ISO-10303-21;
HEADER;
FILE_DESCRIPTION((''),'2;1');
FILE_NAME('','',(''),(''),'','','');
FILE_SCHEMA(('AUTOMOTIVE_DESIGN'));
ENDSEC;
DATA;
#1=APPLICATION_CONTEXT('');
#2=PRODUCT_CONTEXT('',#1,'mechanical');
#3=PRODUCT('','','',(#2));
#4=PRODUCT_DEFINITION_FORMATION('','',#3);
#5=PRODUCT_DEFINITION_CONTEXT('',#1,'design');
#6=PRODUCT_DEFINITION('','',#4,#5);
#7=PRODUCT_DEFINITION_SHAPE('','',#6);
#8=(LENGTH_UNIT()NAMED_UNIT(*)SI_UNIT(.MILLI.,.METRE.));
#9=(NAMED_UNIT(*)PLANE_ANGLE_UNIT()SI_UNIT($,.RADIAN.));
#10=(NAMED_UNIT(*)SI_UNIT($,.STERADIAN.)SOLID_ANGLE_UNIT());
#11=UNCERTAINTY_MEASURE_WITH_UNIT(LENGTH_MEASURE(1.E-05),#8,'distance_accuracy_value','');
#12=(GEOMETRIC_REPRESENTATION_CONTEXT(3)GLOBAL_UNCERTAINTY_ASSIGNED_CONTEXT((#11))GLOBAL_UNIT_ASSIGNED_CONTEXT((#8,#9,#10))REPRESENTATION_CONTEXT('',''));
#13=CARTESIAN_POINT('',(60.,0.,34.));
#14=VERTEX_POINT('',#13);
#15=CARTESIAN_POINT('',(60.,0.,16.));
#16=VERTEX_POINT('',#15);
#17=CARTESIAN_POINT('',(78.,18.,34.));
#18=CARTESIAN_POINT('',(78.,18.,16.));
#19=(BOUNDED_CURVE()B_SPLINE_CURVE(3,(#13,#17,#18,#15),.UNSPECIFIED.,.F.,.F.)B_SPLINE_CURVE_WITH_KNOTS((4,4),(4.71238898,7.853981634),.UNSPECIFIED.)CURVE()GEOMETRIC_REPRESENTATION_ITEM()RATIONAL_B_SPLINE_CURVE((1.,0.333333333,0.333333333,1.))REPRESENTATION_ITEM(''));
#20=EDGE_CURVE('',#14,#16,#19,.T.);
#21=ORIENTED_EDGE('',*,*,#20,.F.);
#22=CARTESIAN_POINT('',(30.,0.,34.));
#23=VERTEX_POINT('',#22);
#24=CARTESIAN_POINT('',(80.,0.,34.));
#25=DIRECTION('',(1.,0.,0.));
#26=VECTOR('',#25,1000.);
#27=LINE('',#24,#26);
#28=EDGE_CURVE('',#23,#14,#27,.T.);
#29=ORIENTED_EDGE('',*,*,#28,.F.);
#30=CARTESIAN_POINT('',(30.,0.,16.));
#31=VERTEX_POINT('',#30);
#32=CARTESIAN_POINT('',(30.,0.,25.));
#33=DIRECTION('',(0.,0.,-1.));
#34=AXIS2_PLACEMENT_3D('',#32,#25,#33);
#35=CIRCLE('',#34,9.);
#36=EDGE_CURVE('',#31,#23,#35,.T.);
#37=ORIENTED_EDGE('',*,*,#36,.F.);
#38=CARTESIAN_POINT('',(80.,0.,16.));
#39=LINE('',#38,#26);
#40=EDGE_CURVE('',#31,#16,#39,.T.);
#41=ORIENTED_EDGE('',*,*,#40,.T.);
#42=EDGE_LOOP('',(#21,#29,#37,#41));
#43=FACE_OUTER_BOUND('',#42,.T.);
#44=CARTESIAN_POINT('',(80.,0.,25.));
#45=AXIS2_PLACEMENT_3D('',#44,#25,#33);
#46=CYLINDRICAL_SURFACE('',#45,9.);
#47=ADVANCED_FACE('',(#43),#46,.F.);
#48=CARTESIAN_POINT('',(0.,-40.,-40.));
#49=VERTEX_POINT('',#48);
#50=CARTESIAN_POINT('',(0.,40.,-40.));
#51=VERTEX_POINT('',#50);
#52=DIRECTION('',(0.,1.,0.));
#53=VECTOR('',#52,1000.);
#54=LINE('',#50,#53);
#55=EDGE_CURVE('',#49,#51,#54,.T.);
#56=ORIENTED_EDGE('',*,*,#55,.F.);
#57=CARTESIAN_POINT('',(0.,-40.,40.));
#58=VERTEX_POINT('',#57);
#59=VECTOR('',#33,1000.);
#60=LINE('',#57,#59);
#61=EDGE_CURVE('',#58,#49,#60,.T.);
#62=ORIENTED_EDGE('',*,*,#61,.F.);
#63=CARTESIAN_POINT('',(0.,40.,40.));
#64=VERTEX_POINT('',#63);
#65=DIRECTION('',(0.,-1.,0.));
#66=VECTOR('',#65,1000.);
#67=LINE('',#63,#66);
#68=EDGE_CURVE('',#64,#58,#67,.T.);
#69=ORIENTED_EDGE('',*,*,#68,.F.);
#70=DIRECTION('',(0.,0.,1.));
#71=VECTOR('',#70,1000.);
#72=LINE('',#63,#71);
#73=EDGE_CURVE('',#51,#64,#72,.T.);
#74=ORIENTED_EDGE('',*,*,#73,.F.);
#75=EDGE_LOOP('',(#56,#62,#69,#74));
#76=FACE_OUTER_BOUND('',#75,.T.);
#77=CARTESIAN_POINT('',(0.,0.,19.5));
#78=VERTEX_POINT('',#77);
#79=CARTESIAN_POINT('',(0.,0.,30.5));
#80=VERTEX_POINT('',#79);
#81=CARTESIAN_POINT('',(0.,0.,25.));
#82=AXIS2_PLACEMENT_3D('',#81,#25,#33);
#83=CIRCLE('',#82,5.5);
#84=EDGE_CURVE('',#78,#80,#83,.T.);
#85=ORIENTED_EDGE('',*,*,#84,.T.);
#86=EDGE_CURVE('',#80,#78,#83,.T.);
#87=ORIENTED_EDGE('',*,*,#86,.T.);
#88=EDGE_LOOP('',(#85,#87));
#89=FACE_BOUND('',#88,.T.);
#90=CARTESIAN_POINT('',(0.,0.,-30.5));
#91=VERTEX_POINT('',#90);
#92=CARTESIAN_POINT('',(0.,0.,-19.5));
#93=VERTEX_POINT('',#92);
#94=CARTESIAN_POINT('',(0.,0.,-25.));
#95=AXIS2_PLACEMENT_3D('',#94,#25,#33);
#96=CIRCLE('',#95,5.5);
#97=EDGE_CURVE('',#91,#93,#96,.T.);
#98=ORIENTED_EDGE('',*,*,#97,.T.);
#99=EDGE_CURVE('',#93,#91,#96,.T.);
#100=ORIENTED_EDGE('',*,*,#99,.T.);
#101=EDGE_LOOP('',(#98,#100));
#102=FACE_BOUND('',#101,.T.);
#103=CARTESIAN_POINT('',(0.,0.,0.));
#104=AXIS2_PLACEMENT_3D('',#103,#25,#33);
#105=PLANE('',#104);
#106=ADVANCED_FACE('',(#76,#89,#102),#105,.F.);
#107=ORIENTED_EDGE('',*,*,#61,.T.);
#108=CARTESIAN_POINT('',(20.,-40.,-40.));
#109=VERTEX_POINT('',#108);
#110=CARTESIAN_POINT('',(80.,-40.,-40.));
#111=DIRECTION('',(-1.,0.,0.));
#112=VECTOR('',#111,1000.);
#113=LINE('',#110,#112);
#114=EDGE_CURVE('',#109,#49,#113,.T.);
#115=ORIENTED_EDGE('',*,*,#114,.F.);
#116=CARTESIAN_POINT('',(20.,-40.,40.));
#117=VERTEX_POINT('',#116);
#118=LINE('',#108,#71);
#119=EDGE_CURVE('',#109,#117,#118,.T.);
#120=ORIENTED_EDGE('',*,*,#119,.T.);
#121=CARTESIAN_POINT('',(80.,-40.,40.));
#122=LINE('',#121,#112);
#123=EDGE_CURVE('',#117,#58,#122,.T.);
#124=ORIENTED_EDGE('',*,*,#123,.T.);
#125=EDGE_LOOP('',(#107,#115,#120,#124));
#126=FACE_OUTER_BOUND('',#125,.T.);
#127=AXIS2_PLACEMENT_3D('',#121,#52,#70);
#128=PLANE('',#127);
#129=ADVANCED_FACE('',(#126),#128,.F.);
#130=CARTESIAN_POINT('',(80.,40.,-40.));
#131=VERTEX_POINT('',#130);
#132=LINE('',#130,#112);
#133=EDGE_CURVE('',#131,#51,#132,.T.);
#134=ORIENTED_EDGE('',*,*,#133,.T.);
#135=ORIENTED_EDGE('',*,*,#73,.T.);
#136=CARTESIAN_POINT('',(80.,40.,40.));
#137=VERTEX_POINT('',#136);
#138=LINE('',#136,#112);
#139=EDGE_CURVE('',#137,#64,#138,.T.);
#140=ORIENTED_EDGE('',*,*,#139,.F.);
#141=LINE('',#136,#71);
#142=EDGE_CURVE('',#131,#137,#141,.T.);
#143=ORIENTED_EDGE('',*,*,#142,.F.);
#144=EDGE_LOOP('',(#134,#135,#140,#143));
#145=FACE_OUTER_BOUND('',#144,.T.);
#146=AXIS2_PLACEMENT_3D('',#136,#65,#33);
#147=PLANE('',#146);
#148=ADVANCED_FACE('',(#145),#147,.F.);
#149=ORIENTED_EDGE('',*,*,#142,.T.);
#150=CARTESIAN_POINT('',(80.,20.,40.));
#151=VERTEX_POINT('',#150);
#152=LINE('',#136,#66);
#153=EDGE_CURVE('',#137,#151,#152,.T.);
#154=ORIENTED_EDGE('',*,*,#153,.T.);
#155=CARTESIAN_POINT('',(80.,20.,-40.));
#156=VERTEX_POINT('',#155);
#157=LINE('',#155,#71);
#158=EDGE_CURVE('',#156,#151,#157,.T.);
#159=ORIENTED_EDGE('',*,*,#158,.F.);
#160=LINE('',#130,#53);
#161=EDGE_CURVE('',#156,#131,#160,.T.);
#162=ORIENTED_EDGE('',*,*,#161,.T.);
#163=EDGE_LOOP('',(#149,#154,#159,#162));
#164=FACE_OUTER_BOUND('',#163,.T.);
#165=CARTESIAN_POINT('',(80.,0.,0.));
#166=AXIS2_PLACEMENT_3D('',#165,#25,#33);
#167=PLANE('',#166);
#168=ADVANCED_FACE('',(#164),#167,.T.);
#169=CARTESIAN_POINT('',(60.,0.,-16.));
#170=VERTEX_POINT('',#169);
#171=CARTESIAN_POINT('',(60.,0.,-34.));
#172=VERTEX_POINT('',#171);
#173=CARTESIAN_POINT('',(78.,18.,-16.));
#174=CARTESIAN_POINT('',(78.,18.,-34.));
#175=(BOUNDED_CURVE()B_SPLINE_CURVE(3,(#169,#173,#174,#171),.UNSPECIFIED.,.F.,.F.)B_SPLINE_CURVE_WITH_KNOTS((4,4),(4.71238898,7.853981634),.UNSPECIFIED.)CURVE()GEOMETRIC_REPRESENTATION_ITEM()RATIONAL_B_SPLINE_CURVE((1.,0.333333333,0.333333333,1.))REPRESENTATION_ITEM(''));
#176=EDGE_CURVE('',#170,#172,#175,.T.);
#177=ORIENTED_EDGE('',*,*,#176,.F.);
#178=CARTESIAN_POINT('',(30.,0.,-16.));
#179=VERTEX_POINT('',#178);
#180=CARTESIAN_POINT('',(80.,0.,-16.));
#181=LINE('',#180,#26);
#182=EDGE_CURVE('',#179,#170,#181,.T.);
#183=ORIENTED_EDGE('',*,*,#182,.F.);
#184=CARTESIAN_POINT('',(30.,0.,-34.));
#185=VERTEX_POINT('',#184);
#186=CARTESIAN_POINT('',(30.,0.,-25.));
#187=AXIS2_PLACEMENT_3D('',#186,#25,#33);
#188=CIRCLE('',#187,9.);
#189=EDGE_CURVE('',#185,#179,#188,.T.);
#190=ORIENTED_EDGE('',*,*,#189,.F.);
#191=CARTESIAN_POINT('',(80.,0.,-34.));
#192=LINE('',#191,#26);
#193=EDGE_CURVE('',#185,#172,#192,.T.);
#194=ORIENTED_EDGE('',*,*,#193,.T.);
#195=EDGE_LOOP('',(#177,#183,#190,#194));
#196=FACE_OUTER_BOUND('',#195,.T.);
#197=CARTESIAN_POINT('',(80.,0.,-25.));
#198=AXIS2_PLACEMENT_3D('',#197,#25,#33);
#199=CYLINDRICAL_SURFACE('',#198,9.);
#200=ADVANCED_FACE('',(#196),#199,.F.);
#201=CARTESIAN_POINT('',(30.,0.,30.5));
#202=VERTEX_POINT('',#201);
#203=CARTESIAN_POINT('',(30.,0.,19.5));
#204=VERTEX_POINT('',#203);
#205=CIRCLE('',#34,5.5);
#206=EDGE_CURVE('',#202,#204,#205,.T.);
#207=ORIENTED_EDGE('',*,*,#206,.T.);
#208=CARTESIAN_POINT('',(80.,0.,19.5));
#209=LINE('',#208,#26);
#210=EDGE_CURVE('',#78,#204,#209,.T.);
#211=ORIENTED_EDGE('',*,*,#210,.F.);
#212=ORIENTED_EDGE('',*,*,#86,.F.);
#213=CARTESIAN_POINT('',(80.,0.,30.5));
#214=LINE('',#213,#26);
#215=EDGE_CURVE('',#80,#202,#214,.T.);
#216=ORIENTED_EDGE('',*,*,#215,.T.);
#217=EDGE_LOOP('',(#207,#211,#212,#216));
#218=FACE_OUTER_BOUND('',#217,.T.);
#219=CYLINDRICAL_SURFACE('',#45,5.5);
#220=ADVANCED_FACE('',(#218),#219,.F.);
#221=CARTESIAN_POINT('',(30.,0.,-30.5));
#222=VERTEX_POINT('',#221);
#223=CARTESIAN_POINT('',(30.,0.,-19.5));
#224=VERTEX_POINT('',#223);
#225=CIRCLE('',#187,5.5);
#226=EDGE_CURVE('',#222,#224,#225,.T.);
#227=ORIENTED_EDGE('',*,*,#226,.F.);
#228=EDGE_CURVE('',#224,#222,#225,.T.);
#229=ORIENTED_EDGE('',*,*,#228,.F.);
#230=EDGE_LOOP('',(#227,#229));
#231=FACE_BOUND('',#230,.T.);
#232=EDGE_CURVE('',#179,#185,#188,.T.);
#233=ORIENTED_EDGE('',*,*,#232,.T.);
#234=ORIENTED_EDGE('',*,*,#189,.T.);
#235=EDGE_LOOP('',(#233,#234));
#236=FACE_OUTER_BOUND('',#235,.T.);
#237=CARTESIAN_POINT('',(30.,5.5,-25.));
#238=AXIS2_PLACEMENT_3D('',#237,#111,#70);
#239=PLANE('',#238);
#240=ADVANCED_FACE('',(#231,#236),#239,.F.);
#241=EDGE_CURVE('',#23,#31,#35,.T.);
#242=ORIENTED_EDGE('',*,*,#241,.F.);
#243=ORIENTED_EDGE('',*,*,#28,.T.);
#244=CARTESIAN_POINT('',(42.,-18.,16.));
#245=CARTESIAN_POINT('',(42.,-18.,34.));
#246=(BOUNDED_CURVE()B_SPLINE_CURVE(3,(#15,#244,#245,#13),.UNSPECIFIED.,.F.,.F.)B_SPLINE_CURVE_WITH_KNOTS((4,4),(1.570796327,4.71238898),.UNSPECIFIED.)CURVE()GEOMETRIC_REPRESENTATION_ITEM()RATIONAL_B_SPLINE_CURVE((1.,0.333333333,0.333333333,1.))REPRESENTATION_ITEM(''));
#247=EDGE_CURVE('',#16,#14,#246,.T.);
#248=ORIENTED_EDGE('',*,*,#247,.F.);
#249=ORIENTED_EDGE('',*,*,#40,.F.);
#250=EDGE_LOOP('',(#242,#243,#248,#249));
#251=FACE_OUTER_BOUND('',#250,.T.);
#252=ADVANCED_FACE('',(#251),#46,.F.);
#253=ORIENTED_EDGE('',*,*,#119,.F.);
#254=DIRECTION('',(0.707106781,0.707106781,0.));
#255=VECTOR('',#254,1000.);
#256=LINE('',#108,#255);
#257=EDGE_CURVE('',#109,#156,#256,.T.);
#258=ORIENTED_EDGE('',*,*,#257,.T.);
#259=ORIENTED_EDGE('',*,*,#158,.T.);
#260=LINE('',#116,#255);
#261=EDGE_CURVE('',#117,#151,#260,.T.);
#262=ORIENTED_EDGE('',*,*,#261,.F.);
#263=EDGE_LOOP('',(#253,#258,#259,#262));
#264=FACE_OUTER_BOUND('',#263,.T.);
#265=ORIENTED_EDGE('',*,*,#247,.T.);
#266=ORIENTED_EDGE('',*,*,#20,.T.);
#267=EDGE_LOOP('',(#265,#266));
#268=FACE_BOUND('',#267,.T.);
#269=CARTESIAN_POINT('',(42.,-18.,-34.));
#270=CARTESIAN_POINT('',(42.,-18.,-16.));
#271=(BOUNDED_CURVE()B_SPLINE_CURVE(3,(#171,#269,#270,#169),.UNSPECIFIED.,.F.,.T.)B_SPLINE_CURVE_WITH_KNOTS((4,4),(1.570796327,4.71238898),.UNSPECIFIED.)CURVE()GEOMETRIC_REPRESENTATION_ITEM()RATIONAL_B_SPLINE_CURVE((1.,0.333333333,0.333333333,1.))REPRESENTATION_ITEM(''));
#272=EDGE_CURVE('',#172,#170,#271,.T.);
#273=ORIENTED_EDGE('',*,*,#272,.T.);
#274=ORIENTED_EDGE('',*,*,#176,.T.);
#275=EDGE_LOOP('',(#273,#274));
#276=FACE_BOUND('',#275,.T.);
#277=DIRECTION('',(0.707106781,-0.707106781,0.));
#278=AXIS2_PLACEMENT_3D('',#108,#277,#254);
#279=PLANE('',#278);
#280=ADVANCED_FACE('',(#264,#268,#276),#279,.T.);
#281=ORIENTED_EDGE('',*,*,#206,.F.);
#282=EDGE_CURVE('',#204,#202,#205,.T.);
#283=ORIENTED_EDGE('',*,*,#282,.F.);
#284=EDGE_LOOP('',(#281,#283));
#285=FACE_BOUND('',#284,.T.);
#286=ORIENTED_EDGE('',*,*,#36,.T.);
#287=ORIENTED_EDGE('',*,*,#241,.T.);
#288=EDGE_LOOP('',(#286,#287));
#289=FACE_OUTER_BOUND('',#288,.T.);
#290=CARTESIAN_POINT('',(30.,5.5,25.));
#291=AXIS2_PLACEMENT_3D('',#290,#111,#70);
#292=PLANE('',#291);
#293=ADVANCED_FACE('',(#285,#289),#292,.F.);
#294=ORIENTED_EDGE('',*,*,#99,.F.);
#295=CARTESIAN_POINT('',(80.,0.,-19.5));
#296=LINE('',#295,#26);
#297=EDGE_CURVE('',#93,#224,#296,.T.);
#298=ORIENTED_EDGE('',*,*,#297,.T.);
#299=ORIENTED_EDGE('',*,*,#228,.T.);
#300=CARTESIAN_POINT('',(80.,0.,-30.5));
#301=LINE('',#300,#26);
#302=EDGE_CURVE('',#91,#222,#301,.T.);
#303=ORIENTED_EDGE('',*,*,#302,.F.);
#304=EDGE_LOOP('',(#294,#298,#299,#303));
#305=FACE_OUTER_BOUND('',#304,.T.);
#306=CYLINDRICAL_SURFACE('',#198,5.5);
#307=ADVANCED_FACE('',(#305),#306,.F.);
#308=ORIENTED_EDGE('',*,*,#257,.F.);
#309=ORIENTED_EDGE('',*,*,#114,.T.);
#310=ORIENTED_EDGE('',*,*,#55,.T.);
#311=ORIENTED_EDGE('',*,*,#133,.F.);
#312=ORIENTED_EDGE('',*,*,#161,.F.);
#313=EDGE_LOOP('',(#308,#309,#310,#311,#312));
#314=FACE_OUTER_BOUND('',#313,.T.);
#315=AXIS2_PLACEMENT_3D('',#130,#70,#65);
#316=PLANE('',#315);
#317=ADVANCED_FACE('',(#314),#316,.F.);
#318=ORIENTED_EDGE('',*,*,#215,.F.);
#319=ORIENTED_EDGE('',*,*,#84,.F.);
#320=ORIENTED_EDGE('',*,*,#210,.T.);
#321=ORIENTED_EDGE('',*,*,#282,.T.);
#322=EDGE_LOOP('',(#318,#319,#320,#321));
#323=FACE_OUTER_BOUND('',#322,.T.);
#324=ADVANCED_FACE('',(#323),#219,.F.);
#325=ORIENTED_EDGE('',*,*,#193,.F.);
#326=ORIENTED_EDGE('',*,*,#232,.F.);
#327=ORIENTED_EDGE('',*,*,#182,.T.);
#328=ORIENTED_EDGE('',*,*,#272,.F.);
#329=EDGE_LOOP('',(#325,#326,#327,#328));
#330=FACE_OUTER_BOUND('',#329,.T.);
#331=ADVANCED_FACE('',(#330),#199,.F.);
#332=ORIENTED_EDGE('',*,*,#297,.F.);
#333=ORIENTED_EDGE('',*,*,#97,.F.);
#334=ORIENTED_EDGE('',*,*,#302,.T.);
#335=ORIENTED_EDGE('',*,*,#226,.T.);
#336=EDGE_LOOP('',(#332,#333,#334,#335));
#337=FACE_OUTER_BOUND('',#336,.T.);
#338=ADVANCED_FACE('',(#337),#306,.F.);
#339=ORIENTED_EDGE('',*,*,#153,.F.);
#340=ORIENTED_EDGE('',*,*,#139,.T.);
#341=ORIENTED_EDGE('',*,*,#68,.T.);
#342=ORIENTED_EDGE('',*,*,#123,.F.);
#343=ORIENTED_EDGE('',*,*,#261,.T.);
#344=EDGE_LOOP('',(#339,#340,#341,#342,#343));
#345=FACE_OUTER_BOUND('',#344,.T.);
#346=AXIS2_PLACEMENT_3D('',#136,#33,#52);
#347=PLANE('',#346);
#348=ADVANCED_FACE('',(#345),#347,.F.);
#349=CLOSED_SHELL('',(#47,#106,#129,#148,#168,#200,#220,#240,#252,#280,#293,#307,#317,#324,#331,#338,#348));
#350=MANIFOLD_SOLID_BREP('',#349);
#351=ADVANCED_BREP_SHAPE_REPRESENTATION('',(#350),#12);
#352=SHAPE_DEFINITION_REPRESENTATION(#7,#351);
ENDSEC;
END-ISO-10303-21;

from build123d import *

# Parameters (mm, degrees)
SKETCH_1_W                = 80
SKETCH_1_H                = 80
EXTRUDE_1_DEPTH           = 80
HOLE_WIZARD_1_D           = 11
HOLE_WIZARD_1_CBORE_D     = 18
HOLE_WIZARD_1_CBORE_DEPTH = 50
CUT_EXTRUDE_1_DEPTH       = 121


with BuildPart() as part:
    # 草图1 → 凸台-拉伸1 (new body)
    with BuildSketch(Plane(origin=(0, 0, 0), x_dir=(0, 0, -1), z_dir=(1, 0, 0))):
        Rectangle(SKETCH_1_W, SKETCH_1_H)
    extrude(amount=EXTRUDE_1_DEPTH)

    # 打孔尺寸(%根据)内六角圆柱头螺钉的类型1 (through all)
    with Locations(Plane(origin=(80, 0, 0), x_dir=(0, 0, -1), z_dir=(1, 0, 0))):
        with Locations((-25, 0), (25, 0)):
            CounterBoreHole(HOLE_WIZARD_1_D / 2, HOLE_WIZARD_1_CBORE_D / 2, HOLE_WIZARD_1_CBORE_DEPTH)

    # 草图2 → 切除-拉伸1 (cut, through all)
    with BuildSketch(Plane.XY.offset(40)):
        Polygon((20, -40), (80, 20), (80, -40), align=None)
    extrude(amount=-CUT_EXTRUDE_1_DEPTH, mode=Mode.SUBTRACT)


solid = part.part
